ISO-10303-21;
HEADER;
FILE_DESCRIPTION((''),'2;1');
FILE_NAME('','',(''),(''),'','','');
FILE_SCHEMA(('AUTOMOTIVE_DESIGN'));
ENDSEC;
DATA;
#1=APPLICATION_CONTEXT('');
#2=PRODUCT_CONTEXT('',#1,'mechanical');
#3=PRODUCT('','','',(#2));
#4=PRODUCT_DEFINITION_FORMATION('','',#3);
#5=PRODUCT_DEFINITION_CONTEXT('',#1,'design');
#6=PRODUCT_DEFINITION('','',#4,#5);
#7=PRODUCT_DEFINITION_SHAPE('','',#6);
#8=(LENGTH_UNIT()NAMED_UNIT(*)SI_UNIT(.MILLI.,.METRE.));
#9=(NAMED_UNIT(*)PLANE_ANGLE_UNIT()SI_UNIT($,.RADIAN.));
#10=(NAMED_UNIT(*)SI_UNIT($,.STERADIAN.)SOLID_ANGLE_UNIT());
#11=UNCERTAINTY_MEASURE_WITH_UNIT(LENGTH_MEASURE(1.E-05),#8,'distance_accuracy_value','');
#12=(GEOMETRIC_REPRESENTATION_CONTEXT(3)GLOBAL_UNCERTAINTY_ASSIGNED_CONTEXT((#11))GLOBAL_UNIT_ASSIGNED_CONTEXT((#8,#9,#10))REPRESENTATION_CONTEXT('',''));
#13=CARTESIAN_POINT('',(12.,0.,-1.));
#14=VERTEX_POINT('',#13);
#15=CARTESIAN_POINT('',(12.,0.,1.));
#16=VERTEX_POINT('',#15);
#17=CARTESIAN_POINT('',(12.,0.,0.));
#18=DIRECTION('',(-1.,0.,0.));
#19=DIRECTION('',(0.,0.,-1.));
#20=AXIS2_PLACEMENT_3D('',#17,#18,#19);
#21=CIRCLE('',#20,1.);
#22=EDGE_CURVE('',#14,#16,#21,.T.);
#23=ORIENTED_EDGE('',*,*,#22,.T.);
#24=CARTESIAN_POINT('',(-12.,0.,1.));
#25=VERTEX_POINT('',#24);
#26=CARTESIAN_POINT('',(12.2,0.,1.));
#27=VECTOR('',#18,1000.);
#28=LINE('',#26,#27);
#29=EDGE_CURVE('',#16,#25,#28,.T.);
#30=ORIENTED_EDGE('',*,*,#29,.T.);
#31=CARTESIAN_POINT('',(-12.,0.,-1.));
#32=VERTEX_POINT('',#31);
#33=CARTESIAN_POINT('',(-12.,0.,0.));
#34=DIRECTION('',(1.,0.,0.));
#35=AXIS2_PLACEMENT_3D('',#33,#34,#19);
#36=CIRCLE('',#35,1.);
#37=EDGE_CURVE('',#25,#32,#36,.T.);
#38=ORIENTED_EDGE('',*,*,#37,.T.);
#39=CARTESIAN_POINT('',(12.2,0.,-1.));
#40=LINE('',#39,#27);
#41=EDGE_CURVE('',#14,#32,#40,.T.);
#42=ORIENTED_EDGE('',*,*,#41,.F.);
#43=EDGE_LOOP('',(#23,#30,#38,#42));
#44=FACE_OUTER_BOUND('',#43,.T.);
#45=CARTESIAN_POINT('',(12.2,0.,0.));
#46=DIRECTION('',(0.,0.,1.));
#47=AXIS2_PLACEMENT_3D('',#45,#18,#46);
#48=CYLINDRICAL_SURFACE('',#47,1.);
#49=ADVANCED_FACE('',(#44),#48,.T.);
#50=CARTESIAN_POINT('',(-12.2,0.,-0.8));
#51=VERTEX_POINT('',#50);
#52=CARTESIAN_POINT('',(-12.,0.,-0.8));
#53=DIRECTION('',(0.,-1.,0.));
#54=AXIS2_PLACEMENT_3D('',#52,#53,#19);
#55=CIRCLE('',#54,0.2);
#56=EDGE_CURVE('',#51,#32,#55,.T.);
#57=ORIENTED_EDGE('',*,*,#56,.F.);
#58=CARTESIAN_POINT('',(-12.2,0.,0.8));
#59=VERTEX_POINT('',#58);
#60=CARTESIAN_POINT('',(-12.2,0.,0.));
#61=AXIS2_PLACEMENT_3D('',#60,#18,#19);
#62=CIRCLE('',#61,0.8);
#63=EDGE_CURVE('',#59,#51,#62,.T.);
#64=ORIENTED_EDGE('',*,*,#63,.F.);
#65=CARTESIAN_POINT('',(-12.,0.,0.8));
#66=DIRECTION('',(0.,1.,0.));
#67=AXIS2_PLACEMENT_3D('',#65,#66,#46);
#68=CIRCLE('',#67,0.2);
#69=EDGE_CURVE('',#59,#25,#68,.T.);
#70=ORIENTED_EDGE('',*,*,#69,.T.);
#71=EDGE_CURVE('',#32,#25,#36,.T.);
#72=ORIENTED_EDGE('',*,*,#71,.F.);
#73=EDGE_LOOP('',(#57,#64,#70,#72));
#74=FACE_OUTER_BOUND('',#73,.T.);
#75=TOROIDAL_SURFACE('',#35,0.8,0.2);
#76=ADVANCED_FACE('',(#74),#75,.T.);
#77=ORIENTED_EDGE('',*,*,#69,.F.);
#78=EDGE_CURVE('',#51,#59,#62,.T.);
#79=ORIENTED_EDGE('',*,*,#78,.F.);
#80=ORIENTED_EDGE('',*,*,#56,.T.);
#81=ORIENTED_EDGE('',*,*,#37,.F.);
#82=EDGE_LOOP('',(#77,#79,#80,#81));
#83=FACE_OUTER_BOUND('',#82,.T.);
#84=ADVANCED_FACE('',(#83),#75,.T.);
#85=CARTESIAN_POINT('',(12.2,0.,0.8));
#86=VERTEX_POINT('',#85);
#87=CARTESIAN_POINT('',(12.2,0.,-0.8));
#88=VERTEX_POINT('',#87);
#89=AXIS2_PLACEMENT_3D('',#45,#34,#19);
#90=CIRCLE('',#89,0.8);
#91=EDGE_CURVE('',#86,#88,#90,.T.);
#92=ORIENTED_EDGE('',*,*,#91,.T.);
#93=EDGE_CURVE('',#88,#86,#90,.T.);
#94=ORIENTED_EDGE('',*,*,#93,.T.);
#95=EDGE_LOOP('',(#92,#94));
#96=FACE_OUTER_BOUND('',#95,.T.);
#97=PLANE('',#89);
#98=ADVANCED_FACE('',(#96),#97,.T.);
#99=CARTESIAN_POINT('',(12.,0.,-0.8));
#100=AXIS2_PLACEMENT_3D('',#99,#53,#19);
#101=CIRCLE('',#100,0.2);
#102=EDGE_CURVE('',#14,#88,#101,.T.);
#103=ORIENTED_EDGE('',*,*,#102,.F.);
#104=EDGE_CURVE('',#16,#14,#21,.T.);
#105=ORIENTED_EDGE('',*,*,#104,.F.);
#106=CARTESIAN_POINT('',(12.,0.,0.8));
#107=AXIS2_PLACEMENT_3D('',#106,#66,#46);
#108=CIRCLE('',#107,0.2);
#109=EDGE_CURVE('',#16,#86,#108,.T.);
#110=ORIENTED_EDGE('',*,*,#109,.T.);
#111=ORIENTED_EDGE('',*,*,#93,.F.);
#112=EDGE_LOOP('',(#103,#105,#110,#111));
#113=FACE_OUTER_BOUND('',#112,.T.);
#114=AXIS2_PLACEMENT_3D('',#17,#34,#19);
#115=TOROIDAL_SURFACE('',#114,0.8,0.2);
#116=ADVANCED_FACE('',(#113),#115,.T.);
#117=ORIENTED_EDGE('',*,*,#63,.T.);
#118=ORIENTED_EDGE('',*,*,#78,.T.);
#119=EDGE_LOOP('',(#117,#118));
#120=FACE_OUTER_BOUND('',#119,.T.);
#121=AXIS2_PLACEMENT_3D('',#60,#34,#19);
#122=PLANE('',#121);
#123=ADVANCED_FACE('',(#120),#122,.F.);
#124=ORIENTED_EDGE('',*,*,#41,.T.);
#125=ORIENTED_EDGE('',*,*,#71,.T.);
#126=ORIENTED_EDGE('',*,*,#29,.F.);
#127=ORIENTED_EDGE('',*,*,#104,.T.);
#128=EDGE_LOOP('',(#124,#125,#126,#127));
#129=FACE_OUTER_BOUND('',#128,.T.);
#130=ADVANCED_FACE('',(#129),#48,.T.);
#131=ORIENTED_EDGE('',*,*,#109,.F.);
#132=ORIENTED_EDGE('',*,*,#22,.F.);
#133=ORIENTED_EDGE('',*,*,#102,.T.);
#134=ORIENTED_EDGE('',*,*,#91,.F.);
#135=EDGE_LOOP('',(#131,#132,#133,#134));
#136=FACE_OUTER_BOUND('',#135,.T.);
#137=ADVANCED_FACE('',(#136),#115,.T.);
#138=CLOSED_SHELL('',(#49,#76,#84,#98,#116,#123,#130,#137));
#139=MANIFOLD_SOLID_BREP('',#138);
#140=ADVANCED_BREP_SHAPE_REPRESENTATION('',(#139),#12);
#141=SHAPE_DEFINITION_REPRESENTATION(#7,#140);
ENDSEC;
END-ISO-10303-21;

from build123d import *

# Parameters (mm, degrees)
SKETCH_1_R      = 1
EXTRUDE_1_DEPTH = 12.2
FILLET_1_R      = 0.2


with BuildPart() as part:
    # 草图1 → 凸台-拉伸1 (new, symmetric)
    with BuildSketch(Plane(origin=(0, 0, 0), x_dir=(0, 0, -1), z_dir=(1, 0, 0))):
        Circle(SKETCH_1_R)
    extrude(amount=EXTRUDE_1_DEPTH, both=True)

    # 圆角1
    fillet_1_edges = [part.edges().sort_by_distance(p)[0] for p in [
        (-12.2, 0, 1),
        (12.2, 0, 1),
    ]]
    fillet(fillet_1_edges, radius=FILLET_1_R)


solid = part.part
